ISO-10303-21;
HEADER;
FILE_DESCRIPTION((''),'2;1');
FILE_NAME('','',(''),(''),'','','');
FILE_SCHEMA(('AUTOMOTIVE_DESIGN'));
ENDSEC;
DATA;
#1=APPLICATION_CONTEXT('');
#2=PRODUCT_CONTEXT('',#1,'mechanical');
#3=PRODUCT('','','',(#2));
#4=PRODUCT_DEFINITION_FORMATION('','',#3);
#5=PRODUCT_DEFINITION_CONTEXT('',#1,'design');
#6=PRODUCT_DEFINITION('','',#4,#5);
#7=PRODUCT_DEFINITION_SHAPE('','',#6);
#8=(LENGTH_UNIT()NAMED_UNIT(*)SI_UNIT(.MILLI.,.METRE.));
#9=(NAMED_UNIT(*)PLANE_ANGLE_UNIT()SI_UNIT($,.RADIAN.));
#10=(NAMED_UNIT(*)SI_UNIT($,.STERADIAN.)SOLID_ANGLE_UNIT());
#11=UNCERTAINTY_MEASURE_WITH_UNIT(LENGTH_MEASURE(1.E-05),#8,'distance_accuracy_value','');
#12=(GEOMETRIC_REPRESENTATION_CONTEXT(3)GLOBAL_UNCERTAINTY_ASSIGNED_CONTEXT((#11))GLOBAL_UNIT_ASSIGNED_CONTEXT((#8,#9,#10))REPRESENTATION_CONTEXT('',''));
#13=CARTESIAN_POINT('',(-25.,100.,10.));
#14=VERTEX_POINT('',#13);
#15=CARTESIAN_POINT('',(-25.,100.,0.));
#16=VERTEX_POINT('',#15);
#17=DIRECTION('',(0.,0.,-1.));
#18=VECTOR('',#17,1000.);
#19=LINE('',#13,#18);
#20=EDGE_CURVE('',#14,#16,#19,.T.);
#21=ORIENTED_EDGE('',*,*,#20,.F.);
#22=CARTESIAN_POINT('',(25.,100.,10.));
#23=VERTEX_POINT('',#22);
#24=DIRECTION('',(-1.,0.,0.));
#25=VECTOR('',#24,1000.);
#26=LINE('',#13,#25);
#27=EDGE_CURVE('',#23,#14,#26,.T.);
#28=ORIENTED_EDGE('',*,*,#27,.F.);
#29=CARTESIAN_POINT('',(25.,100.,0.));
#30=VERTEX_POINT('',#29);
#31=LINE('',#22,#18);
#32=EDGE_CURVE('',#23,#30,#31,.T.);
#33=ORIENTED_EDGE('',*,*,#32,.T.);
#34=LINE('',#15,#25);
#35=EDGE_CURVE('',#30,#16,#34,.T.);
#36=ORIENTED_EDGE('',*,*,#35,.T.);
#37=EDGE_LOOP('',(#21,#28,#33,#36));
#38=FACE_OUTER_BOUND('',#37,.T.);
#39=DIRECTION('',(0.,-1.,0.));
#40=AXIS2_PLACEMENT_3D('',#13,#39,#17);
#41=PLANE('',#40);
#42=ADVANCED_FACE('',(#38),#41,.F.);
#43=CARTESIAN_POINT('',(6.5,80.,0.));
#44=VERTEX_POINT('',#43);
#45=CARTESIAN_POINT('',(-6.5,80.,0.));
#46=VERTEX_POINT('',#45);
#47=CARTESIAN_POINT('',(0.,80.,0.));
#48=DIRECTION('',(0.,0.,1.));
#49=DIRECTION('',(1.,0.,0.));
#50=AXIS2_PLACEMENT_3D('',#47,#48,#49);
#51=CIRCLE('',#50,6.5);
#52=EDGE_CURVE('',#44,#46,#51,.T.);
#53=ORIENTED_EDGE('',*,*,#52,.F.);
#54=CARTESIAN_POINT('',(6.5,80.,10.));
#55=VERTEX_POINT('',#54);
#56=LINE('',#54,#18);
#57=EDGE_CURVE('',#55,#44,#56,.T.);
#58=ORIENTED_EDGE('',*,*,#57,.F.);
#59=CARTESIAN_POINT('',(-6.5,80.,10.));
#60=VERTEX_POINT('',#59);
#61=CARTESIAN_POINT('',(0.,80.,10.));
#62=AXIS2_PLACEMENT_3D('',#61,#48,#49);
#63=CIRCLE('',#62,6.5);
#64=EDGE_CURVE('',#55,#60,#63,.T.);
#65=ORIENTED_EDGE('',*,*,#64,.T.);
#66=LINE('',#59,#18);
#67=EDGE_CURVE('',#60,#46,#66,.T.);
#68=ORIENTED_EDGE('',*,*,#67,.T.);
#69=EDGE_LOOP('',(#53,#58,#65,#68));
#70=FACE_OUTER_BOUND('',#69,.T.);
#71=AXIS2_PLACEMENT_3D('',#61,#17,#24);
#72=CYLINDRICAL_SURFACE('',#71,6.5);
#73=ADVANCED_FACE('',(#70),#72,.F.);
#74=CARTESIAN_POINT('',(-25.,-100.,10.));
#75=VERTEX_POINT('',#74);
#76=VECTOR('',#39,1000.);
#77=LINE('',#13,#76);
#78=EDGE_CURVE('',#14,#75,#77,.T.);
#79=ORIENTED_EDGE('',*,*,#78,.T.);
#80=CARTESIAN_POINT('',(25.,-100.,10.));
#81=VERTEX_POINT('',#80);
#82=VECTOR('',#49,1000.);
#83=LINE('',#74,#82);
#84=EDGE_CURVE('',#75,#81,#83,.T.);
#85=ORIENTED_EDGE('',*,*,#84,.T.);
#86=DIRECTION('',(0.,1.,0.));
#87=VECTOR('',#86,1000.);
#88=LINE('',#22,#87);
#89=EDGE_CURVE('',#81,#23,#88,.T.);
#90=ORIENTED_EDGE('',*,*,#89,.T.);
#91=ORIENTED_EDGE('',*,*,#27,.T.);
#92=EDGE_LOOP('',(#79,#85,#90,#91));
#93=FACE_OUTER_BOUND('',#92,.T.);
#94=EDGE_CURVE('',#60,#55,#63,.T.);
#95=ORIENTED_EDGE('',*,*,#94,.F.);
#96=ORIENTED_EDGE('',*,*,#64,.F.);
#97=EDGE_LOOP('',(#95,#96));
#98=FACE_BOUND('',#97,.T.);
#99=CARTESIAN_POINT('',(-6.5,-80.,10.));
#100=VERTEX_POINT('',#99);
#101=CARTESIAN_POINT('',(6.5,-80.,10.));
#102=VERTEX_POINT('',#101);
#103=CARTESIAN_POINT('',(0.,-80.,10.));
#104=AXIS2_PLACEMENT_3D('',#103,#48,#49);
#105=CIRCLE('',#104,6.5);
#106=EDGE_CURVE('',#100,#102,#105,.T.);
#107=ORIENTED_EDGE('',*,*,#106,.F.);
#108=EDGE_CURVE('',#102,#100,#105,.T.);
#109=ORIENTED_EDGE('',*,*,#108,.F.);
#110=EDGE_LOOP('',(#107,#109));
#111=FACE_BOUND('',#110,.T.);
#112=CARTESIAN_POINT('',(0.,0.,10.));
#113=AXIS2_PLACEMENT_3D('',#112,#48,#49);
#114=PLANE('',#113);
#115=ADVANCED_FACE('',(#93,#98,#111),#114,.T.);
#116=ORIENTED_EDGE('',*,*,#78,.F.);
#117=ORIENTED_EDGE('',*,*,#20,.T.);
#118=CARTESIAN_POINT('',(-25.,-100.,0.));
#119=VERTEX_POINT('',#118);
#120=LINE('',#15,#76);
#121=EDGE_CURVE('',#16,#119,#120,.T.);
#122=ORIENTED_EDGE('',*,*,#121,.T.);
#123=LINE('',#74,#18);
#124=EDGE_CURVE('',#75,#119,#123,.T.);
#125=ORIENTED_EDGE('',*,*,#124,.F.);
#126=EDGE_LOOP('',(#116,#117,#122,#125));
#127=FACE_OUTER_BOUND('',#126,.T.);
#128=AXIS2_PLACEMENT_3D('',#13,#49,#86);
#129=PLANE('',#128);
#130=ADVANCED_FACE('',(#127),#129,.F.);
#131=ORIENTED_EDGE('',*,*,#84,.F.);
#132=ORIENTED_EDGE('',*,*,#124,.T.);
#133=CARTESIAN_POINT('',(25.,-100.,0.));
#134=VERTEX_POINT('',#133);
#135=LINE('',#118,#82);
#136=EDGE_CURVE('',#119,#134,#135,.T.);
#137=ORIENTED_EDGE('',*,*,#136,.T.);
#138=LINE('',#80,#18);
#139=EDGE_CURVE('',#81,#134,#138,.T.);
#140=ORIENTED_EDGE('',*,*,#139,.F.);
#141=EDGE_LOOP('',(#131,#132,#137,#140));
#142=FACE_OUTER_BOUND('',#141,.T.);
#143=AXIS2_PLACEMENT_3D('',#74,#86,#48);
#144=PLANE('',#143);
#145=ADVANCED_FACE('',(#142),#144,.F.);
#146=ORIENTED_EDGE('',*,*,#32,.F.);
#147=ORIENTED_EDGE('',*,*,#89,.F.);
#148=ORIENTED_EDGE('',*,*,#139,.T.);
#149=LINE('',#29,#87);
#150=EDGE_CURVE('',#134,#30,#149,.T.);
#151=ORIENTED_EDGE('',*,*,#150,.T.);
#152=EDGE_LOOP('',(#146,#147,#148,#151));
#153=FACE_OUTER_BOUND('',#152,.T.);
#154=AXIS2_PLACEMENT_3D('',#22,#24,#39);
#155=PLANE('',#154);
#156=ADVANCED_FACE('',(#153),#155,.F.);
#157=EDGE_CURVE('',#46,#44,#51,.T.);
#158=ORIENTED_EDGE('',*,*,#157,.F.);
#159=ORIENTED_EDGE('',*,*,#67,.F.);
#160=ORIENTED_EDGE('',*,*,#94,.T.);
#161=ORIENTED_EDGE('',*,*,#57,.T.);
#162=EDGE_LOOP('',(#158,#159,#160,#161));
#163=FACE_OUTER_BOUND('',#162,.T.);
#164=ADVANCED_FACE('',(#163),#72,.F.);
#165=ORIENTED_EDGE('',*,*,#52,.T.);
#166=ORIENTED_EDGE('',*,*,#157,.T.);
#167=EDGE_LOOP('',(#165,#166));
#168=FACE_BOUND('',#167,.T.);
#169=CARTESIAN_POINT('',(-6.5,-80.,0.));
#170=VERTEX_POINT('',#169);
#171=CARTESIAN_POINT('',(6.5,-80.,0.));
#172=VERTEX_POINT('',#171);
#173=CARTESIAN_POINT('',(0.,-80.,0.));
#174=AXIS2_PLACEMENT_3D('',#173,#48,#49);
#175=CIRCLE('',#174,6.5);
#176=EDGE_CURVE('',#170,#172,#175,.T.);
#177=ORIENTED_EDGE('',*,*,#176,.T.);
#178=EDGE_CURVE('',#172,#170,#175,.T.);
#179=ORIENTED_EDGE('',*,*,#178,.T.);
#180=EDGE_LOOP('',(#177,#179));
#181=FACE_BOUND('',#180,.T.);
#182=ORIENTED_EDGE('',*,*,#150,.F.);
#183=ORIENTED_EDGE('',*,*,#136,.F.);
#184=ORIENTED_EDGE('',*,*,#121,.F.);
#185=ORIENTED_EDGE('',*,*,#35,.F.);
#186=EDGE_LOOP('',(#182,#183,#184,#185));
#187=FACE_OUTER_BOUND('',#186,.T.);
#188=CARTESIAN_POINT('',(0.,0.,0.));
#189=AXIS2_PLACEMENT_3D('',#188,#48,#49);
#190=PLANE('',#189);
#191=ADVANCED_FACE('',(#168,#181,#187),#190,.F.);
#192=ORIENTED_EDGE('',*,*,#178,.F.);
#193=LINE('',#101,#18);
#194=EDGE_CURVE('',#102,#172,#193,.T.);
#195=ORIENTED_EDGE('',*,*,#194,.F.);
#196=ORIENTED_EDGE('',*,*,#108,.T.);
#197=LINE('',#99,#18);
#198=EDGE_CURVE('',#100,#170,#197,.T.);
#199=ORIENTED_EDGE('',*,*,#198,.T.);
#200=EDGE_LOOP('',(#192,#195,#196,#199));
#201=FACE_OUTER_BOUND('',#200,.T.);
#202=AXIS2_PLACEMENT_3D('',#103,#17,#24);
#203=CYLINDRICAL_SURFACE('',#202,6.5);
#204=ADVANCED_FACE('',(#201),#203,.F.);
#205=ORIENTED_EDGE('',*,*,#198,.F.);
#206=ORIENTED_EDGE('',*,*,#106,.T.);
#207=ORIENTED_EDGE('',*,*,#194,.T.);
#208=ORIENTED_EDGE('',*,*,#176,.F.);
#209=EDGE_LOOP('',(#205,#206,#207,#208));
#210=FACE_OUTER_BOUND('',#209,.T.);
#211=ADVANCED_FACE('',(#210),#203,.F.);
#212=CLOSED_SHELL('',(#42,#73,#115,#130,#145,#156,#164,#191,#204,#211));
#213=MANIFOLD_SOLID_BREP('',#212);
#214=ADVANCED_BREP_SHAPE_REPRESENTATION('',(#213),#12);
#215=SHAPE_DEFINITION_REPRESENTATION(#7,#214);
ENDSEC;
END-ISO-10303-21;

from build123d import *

# Parameters (mm, degrees)
SKETCH_1_W      = 50
SKETCH_1_H      = 200
SKETCH_1_R      = 6.5
EXTRUDE_1_DEPTH = 10


with BuildPart() as part:
    # 草图1 → 凸台-拉伸1 (new body)
    with BuildSketch(Plane.XY):
        Rectangle(SKETCH_1_W, SKETCH_1_H)
        with Locations((0, 80)):
            Circle(SKETCH_1_R, mode=Mode.SUBTRACT)
        with Locations((0, -80)):
            Circle(SKETCH_1_R, mode=Mode.SUBTRACT)
    extrude(amount=EXTRUDE_1_DEPTH)


solid = part.part
